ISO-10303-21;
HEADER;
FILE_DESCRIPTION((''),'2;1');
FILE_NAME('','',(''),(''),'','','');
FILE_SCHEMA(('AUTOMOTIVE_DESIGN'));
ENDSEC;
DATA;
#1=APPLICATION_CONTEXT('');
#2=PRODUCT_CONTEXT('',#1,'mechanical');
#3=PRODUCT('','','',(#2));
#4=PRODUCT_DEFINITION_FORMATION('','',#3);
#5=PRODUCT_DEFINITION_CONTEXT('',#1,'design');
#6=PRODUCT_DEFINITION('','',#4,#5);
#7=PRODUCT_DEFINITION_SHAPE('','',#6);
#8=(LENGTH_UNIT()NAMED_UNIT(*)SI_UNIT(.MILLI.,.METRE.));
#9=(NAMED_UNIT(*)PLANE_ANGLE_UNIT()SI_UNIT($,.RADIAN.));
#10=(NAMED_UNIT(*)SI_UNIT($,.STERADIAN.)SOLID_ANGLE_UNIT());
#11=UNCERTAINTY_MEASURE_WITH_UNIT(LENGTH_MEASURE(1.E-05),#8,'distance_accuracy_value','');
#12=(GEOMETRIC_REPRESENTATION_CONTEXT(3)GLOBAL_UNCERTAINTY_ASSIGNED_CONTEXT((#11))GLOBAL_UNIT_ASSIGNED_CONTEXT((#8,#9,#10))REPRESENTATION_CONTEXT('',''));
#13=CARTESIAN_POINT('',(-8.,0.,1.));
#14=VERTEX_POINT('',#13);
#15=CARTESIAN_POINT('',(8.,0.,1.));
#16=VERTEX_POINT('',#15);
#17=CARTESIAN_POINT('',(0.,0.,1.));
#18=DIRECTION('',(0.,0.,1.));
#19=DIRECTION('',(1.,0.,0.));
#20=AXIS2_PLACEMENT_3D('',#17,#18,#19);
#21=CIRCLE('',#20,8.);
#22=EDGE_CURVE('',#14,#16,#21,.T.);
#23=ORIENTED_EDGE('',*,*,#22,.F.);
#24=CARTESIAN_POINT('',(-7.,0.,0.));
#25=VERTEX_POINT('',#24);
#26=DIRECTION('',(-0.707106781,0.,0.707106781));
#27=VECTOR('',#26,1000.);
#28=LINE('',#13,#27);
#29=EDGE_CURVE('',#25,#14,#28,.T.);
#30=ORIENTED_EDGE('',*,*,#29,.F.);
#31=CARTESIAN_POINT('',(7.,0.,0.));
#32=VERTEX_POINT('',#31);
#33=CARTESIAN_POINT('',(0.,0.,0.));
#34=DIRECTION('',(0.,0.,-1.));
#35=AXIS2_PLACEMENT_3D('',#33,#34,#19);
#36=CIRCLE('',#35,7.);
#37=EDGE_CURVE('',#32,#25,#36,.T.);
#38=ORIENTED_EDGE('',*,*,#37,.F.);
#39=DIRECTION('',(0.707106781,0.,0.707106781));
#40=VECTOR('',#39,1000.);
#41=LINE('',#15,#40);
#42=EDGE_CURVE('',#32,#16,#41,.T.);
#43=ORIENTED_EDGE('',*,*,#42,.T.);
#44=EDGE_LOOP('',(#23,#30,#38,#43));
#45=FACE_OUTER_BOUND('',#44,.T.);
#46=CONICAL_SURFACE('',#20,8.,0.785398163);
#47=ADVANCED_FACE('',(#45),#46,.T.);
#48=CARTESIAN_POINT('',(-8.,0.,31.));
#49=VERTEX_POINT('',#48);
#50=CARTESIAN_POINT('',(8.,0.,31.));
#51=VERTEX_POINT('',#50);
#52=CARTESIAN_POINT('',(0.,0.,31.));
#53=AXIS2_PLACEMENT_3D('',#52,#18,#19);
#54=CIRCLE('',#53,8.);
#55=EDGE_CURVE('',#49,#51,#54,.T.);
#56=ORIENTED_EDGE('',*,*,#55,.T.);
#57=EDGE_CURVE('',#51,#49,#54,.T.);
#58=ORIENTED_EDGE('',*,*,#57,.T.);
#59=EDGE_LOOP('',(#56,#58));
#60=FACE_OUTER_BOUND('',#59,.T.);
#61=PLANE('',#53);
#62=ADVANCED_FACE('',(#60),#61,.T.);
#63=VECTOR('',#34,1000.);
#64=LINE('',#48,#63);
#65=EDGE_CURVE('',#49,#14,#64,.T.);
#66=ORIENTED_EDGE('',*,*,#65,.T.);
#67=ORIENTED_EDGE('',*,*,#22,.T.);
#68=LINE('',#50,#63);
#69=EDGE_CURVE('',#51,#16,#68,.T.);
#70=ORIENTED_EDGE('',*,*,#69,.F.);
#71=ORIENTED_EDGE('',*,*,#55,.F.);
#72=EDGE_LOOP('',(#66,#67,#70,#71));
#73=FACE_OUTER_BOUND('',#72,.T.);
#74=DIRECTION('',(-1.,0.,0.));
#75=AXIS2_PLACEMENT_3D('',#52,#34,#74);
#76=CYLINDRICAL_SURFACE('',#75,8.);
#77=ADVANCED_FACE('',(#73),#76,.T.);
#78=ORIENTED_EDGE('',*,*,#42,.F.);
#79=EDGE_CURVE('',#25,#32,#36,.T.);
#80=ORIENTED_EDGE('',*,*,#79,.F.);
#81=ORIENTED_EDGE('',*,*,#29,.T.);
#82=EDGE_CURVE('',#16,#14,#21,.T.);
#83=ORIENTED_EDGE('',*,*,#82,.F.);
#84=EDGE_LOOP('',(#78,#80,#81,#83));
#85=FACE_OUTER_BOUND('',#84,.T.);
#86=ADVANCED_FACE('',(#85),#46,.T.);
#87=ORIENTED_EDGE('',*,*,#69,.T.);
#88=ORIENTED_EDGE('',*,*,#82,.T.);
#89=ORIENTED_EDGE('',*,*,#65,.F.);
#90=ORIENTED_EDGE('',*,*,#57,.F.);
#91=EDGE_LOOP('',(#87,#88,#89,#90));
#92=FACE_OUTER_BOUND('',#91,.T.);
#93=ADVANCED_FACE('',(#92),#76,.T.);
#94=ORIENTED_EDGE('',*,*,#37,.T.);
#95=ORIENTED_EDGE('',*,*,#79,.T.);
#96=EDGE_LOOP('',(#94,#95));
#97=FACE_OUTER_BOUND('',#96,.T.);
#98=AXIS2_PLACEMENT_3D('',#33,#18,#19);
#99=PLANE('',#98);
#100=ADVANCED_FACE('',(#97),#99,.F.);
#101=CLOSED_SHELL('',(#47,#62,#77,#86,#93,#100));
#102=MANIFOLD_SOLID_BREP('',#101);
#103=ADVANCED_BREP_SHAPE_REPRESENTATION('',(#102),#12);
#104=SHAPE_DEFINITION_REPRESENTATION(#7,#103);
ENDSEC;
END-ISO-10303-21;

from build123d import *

# Parameters (mm, degrees)
SKETCH1_R           = 8
BOSS_EXTRUDE1_DEPTH = 31
CHAMFER2_SIZE       = 1


with BuildPart() as part:
    # Sketch1 → Boss-Extrude1 (new body)
    with BuildSketch(Plane.XY):
        Circle(SKETCH1_R)
    extrude(amount=BOSS_EXTRUDE1_DEPTH)

    # Chamfer2
    chamfer2_edges = [part.edges().sort_by_distance(p)[0] for p in [
        (-8, 0, 0),
    ]]
    chamfer(chamfer2_edges, length=CHAMFER2_SIZE)


solid = part.part
